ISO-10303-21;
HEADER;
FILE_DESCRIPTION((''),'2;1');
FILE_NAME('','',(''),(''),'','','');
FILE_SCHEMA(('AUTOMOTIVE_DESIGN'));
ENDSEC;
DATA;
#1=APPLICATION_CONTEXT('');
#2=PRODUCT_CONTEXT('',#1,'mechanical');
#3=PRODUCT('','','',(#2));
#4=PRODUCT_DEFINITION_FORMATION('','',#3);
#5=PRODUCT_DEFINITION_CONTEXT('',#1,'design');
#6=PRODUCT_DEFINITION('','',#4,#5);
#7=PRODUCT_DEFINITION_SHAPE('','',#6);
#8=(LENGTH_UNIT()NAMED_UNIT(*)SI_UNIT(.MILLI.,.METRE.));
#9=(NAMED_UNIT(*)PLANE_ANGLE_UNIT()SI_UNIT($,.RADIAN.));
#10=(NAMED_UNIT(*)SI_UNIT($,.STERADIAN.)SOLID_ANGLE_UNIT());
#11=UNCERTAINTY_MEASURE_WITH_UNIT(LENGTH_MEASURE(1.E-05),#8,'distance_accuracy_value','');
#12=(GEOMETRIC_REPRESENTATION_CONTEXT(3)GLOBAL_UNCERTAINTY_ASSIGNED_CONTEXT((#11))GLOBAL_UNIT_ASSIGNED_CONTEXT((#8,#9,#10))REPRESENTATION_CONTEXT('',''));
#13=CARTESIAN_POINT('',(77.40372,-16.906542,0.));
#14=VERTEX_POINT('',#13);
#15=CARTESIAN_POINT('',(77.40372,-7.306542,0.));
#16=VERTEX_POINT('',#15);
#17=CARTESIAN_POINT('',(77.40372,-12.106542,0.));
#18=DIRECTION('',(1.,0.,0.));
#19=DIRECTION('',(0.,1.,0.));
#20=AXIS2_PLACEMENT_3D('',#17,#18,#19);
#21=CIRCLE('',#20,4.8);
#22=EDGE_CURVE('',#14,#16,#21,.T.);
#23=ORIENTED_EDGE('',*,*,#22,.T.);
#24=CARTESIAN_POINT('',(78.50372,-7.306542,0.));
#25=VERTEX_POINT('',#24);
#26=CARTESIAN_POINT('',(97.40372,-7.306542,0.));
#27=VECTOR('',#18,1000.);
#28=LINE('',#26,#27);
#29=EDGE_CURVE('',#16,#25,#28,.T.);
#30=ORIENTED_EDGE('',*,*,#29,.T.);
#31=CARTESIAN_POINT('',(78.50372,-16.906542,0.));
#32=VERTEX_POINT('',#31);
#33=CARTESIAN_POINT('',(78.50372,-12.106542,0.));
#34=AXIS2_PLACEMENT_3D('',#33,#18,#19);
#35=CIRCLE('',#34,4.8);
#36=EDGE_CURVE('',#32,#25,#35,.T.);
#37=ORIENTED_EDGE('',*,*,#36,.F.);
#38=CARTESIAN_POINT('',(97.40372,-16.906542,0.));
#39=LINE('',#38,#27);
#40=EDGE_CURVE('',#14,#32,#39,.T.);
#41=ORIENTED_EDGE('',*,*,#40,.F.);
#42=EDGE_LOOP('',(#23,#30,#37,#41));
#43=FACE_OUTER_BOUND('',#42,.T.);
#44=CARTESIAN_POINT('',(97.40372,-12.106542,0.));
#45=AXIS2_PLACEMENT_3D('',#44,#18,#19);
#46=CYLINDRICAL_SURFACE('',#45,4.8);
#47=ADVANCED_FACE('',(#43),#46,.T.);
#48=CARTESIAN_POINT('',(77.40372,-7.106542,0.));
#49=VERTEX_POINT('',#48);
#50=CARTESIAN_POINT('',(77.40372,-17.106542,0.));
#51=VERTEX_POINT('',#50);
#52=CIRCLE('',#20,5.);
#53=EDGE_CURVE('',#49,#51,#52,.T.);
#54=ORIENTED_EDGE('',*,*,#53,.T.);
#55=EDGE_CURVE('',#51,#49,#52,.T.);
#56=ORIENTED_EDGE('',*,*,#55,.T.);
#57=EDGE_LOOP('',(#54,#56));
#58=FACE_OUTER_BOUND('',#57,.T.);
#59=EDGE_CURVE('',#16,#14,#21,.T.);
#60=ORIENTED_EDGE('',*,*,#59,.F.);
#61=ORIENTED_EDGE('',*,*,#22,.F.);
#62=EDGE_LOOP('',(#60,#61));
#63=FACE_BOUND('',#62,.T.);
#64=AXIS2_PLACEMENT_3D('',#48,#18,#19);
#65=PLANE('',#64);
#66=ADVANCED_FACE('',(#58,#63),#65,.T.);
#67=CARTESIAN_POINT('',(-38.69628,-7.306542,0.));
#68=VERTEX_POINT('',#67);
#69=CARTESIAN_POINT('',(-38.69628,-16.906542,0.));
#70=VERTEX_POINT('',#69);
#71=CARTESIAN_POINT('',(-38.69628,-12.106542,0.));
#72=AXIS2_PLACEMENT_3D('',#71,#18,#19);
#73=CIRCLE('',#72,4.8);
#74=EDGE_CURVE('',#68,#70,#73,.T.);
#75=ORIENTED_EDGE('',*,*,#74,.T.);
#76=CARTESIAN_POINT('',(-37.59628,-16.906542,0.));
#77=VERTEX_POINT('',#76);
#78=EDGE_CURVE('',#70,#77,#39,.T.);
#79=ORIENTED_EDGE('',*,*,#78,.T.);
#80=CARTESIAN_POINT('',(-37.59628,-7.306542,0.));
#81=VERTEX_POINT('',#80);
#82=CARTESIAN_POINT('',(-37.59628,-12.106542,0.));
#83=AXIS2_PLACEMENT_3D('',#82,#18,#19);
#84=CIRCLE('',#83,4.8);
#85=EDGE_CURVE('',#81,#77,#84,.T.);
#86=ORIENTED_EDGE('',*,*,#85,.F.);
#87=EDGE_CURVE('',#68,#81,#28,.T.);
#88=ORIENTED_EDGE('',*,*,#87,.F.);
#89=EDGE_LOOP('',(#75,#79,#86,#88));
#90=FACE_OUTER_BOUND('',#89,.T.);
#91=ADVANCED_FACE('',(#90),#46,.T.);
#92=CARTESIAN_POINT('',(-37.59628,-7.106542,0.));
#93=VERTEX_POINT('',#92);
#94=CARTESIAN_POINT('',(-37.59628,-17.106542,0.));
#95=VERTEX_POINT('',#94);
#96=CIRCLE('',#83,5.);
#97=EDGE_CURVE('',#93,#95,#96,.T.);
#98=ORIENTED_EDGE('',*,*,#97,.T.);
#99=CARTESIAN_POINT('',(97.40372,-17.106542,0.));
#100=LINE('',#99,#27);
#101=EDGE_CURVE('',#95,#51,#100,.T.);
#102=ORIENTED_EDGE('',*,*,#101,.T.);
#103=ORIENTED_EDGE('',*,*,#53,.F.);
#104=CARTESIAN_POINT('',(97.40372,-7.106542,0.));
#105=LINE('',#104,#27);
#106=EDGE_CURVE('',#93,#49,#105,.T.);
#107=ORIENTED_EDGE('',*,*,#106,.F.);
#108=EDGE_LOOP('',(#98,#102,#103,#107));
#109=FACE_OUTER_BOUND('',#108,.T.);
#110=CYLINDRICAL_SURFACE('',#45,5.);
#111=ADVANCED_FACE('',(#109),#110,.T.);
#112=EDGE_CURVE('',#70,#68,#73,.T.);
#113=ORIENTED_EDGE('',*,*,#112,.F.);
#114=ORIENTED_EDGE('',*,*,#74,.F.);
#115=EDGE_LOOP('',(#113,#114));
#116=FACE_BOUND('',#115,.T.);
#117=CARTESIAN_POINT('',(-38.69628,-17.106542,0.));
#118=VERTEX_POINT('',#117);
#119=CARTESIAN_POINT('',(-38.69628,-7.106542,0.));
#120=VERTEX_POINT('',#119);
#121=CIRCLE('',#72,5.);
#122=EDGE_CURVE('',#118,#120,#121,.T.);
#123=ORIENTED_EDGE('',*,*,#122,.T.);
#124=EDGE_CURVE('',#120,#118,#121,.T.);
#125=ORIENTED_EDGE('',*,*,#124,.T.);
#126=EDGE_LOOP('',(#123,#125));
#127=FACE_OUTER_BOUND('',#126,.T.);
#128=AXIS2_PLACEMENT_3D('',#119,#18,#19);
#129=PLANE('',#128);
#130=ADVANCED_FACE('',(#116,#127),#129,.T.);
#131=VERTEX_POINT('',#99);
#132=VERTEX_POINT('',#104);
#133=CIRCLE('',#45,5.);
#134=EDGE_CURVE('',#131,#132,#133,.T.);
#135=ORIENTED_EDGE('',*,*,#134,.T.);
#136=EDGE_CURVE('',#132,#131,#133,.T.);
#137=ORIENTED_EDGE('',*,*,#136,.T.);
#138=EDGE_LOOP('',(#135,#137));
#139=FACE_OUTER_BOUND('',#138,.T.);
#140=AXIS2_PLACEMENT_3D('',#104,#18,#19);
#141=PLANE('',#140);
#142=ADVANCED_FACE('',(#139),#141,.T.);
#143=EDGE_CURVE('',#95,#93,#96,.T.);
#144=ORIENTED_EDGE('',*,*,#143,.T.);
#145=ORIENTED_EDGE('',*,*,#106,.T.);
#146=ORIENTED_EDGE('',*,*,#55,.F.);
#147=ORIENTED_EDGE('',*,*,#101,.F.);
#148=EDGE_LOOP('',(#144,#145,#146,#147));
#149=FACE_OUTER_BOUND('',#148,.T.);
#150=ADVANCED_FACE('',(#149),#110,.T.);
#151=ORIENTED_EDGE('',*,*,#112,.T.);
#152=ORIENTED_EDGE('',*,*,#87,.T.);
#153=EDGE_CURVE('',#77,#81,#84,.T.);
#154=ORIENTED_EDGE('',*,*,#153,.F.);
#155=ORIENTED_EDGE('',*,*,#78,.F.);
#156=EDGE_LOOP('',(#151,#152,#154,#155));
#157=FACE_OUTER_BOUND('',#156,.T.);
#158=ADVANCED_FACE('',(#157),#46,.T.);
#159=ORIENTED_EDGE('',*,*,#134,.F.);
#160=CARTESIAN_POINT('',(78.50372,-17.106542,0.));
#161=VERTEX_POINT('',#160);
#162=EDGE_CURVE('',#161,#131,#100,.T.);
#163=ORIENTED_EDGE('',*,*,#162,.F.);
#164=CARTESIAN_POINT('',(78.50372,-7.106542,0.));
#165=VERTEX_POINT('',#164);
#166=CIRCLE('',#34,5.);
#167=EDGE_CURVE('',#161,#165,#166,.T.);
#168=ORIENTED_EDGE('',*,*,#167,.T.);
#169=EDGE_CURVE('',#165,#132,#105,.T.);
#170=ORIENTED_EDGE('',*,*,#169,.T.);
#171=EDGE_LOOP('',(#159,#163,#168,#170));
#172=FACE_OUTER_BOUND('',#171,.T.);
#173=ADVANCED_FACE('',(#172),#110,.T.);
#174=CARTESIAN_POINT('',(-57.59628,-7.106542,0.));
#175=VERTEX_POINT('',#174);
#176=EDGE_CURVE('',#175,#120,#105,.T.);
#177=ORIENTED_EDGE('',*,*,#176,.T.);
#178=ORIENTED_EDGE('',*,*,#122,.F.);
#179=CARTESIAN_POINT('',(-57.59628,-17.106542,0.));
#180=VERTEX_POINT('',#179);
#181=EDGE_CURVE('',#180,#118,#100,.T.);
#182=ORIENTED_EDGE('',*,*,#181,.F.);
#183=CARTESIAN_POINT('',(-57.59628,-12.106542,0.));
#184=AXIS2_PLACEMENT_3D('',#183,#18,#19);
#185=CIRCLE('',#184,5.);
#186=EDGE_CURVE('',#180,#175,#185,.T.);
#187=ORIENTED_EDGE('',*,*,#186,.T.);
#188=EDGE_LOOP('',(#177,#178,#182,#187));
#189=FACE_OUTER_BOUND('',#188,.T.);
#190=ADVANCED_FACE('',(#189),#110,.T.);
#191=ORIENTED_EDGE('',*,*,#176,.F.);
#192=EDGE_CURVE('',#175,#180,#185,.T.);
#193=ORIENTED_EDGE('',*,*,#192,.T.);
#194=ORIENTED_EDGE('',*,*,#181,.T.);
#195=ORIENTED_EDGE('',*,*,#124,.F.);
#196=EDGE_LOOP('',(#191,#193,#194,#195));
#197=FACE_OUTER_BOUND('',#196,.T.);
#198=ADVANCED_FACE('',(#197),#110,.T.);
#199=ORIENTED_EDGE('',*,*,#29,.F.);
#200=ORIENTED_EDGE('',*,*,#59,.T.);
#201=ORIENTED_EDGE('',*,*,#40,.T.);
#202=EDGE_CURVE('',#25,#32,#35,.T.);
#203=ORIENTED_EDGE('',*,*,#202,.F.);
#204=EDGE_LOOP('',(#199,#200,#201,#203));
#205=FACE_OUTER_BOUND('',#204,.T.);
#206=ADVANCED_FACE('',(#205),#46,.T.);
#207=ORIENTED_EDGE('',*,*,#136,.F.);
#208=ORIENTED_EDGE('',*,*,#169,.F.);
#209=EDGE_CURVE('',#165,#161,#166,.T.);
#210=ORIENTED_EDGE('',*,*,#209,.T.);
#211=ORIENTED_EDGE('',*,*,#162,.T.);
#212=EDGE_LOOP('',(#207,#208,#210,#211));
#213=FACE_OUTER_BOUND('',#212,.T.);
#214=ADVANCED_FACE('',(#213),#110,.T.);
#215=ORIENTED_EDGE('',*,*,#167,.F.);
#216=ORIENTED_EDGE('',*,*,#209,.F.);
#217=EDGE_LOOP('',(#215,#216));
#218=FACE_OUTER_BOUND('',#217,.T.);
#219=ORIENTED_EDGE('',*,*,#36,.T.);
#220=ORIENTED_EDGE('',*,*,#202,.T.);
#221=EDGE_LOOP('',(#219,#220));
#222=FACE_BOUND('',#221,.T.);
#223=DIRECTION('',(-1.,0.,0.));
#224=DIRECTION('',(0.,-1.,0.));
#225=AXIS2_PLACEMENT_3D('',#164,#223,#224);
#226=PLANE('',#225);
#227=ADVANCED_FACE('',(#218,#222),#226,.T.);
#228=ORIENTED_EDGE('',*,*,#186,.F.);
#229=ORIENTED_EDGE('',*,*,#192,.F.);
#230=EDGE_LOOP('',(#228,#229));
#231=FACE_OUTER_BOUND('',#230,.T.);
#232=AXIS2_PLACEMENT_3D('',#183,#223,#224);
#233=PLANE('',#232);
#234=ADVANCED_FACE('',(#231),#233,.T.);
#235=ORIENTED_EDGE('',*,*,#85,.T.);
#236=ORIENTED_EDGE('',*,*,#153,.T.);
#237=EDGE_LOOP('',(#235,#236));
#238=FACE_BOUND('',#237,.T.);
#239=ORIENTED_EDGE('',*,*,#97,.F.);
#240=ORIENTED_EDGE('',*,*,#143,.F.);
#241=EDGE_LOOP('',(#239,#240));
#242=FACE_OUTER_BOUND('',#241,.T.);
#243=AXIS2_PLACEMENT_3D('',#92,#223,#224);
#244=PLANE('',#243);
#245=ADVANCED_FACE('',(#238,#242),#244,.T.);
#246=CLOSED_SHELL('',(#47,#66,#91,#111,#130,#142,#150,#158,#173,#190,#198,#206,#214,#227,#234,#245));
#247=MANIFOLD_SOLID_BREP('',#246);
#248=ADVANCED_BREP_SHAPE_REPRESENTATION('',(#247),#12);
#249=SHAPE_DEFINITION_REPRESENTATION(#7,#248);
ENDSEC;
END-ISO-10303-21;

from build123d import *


with BuildPart() as part:
    # Sketch1 → Revolve1 (revolve)
    with BuildSketch(Plane.XY):
        Polygon((-57.596279733, -12.106542056), (-57.596279733, -7.106542056), (-38.696279733, -7.106542056), (-38.696279733, -7.306542056), (-37.596279733, -7.306542056), (-37.596279733, -7.106542056), (77.403720267, -7.106542056), (77.403720267, -7.306542056), (78.503720267, -7.306542056), (78.503720267, -7.106542056), (97.403720267, -7.106542056), (97.403720267, -12.106542056), align=None)
    revolve(axis=Axis((97.403720267, -12.106542056, 0), (-1, 0, 0)))


solid = part.part
